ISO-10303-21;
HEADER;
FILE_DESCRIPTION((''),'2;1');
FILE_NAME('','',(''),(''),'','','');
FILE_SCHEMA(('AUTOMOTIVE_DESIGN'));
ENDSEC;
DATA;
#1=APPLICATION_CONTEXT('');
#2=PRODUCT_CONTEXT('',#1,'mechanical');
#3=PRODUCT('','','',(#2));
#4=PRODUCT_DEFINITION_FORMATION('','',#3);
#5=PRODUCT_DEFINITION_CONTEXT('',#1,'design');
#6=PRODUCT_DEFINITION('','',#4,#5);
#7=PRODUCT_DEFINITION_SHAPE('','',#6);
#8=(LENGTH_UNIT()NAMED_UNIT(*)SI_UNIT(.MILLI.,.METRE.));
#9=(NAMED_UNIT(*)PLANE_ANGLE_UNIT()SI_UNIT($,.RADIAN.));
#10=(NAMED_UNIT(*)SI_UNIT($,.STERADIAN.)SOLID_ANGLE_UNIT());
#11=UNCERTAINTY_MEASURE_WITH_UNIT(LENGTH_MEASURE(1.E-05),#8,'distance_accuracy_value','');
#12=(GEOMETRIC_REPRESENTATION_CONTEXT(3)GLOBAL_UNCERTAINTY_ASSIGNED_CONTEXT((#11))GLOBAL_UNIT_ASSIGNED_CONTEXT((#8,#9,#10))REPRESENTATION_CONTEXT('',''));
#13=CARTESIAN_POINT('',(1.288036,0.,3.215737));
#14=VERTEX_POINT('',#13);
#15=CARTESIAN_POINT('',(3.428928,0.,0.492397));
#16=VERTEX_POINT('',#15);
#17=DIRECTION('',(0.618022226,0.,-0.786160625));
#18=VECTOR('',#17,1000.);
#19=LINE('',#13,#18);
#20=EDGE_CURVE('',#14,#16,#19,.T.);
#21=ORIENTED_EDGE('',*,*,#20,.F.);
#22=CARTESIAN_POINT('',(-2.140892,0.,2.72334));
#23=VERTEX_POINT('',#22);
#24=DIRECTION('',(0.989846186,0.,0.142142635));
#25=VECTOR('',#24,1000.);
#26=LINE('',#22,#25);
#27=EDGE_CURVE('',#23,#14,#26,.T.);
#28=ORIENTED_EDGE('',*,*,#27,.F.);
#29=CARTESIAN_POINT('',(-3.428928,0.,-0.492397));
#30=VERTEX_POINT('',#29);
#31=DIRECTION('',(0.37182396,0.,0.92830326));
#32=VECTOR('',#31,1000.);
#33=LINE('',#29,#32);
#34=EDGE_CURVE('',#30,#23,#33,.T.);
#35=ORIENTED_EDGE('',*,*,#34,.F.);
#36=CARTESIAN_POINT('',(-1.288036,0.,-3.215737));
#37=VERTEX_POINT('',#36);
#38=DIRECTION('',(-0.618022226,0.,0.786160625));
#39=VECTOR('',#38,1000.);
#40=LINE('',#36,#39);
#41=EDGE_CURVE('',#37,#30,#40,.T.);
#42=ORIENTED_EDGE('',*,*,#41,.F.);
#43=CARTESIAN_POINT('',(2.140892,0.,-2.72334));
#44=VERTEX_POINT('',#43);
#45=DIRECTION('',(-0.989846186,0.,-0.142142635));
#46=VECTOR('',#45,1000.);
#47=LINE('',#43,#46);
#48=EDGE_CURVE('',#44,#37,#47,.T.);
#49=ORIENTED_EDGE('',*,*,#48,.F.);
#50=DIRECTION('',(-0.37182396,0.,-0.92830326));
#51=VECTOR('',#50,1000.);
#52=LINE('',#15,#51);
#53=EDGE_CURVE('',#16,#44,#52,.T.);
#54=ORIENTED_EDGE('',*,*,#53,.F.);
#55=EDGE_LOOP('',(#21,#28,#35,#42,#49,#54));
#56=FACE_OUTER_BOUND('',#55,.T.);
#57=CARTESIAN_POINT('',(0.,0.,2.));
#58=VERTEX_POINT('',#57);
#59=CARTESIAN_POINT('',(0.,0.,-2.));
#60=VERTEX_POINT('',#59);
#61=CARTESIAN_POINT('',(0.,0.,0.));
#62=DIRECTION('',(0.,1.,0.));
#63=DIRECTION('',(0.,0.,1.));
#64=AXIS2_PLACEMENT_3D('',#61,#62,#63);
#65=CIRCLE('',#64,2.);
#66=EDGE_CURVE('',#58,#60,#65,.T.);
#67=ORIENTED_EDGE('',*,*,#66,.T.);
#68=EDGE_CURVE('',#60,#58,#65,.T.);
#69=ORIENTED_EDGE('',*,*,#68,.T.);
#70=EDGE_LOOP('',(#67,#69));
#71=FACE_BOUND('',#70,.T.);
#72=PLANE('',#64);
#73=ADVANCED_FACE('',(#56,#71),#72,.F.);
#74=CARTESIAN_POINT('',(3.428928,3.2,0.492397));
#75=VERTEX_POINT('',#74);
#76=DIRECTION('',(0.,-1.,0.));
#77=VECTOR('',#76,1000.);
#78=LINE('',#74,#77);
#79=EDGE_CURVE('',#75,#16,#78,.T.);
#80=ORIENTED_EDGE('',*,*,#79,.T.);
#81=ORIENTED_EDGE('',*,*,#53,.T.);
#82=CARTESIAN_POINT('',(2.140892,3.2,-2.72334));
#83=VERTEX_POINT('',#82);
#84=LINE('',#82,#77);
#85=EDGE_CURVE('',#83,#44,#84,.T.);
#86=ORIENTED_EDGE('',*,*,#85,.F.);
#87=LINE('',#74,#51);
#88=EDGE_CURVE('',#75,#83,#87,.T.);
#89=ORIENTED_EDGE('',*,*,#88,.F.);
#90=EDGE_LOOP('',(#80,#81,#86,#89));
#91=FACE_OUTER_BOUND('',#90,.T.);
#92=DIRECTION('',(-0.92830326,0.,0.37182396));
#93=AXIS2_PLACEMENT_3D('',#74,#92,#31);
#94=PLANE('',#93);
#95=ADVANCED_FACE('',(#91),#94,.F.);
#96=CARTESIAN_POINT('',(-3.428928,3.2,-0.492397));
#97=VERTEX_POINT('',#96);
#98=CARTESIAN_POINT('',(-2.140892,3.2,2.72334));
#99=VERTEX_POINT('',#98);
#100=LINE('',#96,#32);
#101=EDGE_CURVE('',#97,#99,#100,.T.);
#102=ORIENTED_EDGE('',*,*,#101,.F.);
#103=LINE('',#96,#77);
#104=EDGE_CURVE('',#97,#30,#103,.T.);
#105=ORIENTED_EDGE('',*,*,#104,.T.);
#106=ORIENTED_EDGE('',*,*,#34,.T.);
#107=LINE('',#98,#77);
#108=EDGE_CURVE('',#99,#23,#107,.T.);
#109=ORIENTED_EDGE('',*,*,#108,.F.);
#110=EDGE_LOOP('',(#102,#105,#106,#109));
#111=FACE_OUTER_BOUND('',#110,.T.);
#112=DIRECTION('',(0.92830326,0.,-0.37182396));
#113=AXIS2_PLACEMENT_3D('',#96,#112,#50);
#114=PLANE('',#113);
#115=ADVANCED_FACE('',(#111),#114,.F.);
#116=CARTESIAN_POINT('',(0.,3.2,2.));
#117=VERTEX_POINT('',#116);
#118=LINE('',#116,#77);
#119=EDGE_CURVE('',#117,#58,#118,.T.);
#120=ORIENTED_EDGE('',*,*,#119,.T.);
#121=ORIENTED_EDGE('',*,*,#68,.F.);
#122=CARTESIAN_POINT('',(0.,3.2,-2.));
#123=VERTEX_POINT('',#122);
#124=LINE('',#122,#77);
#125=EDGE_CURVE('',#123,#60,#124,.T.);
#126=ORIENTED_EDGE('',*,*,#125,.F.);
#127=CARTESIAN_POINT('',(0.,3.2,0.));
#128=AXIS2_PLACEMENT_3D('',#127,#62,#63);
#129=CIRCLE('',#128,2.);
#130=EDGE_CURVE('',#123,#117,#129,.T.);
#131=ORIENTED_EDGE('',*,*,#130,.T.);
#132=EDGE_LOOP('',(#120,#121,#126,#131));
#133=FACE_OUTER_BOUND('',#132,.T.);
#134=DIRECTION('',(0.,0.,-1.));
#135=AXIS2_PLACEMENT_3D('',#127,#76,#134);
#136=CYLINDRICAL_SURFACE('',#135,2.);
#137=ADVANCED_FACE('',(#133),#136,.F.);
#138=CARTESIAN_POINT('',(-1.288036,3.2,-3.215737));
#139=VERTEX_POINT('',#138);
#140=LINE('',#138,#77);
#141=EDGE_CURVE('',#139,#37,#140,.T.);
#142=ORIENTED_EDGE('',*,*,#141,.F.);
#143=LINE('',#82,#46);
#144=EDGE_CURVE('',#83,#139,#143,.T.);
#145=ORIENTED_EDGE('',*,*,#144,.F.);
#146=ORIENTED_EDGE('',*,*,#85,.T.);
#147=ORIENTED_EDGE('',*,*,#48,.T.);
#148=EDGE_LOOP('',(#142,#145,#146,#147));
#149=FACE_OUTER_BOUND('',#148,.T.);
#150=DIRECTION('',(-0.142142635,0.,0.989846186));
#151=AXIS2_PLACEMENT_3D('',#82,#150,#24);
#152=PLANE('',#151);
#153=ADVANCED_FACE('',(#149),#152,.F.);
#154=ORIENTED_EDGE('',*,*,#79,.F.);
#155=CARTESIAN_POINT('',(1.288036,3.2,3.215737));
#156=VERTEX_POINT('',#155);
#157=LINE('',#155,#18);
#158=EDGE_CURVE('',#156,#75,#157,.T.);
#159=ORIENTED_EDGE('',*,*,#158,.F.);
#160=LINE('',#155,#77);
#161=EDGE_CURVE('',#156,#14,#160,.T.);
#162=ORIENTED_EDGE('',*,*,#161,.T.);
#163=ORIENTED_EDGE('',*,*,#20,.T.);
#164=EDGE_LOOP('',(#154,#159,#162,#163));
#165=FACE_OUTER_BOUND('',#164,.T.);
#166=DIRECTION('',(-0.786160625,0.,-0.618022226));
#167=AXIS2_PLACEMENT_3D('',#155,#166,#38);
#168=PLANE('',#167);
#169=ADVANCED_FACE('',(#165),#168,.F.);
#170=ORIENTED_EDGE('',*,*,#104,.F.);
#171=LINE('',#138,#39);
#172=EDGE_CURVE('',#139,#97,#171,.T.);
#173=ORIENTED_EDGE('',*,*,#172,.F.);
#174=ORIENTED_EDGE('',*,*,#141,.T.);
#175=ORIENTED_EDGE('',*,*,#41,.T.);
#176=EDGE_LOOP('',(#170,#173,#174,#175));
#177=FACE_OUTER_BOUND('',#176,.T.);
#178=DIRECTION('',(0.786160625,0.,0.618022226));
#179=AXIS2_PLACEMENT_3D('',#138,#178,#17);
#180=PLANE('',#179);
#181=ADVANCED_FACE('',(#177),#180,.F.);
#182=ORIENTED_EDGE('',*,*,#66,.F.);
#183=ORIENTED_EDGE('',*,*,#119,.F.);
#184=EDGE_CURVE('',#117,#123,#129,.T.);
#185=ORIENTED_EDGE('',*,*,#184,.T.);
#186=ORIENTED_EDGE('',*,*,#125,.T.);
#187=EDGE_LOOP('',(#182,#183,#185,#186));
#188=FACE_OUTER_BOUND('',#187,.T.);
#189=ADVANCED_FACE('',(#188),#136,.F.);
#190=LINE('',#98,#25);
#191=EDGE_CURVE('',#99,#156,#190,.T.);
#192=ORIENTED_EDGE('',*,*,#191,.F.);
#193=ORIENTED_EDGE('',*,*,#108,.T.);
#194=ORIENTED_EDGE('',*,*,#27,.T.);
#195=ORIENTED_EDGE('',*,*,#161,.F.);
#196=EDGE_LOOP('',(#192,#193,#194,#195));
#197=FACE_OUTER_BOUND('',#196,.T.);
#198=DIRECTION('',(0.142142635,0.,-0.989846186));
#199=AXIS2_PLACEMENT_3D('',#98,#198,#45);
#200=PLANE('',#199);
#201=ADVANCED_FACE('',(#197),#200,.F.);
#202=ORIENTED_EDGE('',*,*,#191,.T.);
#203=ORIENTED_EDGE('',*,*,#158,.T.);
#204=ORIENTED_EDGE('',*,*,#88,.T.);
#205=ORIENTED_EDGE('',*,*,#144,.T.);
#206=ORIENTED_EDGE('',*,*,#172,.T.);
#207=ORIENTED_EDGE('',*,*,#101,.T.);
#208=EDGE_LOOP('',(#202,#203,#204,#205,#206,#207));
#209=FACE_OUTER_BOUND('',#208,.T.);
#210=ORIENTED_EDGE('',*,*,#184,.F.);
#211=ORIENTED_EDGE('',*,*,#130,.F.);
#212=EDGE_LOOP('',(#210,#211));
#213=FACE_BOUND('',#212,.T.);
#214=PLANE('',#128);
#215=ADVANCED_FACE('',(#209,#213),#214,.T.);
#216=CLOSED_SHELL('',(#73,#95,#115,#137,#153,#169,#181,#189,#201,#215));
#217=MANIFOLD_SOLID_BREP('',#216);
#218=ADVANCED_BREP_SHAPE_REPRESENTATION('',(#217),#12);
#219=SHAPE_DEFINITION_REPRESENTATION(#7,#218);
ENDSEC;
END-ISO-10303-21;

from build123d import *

# Parameters (mm, degrees)
SKETCH1_R           = 2
BOSS_EXTRUDE1_DEPTH = 3.2


with BuildPart() as part:
    # Sketch1 → Boss-Extrude1 (new body)
    with BuildSketch(Plane(origin=(0, 0, 0), x_dir=(1, 0, 0), z_dir=(0, 1, 0))):
        Polygon((2.14089179, 2.723340292), (-1.288035981, 3.215736823), (-3.428927771, 0.492396531), (-2.14089179, -2.723340292), (1.288035981, -3.215736823), (3.428927771, -0.492396531), align=None)
        with Locations(Location((0, 0, 0), (0, 0, 270))):
            Circle(SKETCH1_R, mode=Mode.SUBTRACT)
    extrude(amount=BOSS_EXTRUDE1_DEPTH)


solid = part.part
